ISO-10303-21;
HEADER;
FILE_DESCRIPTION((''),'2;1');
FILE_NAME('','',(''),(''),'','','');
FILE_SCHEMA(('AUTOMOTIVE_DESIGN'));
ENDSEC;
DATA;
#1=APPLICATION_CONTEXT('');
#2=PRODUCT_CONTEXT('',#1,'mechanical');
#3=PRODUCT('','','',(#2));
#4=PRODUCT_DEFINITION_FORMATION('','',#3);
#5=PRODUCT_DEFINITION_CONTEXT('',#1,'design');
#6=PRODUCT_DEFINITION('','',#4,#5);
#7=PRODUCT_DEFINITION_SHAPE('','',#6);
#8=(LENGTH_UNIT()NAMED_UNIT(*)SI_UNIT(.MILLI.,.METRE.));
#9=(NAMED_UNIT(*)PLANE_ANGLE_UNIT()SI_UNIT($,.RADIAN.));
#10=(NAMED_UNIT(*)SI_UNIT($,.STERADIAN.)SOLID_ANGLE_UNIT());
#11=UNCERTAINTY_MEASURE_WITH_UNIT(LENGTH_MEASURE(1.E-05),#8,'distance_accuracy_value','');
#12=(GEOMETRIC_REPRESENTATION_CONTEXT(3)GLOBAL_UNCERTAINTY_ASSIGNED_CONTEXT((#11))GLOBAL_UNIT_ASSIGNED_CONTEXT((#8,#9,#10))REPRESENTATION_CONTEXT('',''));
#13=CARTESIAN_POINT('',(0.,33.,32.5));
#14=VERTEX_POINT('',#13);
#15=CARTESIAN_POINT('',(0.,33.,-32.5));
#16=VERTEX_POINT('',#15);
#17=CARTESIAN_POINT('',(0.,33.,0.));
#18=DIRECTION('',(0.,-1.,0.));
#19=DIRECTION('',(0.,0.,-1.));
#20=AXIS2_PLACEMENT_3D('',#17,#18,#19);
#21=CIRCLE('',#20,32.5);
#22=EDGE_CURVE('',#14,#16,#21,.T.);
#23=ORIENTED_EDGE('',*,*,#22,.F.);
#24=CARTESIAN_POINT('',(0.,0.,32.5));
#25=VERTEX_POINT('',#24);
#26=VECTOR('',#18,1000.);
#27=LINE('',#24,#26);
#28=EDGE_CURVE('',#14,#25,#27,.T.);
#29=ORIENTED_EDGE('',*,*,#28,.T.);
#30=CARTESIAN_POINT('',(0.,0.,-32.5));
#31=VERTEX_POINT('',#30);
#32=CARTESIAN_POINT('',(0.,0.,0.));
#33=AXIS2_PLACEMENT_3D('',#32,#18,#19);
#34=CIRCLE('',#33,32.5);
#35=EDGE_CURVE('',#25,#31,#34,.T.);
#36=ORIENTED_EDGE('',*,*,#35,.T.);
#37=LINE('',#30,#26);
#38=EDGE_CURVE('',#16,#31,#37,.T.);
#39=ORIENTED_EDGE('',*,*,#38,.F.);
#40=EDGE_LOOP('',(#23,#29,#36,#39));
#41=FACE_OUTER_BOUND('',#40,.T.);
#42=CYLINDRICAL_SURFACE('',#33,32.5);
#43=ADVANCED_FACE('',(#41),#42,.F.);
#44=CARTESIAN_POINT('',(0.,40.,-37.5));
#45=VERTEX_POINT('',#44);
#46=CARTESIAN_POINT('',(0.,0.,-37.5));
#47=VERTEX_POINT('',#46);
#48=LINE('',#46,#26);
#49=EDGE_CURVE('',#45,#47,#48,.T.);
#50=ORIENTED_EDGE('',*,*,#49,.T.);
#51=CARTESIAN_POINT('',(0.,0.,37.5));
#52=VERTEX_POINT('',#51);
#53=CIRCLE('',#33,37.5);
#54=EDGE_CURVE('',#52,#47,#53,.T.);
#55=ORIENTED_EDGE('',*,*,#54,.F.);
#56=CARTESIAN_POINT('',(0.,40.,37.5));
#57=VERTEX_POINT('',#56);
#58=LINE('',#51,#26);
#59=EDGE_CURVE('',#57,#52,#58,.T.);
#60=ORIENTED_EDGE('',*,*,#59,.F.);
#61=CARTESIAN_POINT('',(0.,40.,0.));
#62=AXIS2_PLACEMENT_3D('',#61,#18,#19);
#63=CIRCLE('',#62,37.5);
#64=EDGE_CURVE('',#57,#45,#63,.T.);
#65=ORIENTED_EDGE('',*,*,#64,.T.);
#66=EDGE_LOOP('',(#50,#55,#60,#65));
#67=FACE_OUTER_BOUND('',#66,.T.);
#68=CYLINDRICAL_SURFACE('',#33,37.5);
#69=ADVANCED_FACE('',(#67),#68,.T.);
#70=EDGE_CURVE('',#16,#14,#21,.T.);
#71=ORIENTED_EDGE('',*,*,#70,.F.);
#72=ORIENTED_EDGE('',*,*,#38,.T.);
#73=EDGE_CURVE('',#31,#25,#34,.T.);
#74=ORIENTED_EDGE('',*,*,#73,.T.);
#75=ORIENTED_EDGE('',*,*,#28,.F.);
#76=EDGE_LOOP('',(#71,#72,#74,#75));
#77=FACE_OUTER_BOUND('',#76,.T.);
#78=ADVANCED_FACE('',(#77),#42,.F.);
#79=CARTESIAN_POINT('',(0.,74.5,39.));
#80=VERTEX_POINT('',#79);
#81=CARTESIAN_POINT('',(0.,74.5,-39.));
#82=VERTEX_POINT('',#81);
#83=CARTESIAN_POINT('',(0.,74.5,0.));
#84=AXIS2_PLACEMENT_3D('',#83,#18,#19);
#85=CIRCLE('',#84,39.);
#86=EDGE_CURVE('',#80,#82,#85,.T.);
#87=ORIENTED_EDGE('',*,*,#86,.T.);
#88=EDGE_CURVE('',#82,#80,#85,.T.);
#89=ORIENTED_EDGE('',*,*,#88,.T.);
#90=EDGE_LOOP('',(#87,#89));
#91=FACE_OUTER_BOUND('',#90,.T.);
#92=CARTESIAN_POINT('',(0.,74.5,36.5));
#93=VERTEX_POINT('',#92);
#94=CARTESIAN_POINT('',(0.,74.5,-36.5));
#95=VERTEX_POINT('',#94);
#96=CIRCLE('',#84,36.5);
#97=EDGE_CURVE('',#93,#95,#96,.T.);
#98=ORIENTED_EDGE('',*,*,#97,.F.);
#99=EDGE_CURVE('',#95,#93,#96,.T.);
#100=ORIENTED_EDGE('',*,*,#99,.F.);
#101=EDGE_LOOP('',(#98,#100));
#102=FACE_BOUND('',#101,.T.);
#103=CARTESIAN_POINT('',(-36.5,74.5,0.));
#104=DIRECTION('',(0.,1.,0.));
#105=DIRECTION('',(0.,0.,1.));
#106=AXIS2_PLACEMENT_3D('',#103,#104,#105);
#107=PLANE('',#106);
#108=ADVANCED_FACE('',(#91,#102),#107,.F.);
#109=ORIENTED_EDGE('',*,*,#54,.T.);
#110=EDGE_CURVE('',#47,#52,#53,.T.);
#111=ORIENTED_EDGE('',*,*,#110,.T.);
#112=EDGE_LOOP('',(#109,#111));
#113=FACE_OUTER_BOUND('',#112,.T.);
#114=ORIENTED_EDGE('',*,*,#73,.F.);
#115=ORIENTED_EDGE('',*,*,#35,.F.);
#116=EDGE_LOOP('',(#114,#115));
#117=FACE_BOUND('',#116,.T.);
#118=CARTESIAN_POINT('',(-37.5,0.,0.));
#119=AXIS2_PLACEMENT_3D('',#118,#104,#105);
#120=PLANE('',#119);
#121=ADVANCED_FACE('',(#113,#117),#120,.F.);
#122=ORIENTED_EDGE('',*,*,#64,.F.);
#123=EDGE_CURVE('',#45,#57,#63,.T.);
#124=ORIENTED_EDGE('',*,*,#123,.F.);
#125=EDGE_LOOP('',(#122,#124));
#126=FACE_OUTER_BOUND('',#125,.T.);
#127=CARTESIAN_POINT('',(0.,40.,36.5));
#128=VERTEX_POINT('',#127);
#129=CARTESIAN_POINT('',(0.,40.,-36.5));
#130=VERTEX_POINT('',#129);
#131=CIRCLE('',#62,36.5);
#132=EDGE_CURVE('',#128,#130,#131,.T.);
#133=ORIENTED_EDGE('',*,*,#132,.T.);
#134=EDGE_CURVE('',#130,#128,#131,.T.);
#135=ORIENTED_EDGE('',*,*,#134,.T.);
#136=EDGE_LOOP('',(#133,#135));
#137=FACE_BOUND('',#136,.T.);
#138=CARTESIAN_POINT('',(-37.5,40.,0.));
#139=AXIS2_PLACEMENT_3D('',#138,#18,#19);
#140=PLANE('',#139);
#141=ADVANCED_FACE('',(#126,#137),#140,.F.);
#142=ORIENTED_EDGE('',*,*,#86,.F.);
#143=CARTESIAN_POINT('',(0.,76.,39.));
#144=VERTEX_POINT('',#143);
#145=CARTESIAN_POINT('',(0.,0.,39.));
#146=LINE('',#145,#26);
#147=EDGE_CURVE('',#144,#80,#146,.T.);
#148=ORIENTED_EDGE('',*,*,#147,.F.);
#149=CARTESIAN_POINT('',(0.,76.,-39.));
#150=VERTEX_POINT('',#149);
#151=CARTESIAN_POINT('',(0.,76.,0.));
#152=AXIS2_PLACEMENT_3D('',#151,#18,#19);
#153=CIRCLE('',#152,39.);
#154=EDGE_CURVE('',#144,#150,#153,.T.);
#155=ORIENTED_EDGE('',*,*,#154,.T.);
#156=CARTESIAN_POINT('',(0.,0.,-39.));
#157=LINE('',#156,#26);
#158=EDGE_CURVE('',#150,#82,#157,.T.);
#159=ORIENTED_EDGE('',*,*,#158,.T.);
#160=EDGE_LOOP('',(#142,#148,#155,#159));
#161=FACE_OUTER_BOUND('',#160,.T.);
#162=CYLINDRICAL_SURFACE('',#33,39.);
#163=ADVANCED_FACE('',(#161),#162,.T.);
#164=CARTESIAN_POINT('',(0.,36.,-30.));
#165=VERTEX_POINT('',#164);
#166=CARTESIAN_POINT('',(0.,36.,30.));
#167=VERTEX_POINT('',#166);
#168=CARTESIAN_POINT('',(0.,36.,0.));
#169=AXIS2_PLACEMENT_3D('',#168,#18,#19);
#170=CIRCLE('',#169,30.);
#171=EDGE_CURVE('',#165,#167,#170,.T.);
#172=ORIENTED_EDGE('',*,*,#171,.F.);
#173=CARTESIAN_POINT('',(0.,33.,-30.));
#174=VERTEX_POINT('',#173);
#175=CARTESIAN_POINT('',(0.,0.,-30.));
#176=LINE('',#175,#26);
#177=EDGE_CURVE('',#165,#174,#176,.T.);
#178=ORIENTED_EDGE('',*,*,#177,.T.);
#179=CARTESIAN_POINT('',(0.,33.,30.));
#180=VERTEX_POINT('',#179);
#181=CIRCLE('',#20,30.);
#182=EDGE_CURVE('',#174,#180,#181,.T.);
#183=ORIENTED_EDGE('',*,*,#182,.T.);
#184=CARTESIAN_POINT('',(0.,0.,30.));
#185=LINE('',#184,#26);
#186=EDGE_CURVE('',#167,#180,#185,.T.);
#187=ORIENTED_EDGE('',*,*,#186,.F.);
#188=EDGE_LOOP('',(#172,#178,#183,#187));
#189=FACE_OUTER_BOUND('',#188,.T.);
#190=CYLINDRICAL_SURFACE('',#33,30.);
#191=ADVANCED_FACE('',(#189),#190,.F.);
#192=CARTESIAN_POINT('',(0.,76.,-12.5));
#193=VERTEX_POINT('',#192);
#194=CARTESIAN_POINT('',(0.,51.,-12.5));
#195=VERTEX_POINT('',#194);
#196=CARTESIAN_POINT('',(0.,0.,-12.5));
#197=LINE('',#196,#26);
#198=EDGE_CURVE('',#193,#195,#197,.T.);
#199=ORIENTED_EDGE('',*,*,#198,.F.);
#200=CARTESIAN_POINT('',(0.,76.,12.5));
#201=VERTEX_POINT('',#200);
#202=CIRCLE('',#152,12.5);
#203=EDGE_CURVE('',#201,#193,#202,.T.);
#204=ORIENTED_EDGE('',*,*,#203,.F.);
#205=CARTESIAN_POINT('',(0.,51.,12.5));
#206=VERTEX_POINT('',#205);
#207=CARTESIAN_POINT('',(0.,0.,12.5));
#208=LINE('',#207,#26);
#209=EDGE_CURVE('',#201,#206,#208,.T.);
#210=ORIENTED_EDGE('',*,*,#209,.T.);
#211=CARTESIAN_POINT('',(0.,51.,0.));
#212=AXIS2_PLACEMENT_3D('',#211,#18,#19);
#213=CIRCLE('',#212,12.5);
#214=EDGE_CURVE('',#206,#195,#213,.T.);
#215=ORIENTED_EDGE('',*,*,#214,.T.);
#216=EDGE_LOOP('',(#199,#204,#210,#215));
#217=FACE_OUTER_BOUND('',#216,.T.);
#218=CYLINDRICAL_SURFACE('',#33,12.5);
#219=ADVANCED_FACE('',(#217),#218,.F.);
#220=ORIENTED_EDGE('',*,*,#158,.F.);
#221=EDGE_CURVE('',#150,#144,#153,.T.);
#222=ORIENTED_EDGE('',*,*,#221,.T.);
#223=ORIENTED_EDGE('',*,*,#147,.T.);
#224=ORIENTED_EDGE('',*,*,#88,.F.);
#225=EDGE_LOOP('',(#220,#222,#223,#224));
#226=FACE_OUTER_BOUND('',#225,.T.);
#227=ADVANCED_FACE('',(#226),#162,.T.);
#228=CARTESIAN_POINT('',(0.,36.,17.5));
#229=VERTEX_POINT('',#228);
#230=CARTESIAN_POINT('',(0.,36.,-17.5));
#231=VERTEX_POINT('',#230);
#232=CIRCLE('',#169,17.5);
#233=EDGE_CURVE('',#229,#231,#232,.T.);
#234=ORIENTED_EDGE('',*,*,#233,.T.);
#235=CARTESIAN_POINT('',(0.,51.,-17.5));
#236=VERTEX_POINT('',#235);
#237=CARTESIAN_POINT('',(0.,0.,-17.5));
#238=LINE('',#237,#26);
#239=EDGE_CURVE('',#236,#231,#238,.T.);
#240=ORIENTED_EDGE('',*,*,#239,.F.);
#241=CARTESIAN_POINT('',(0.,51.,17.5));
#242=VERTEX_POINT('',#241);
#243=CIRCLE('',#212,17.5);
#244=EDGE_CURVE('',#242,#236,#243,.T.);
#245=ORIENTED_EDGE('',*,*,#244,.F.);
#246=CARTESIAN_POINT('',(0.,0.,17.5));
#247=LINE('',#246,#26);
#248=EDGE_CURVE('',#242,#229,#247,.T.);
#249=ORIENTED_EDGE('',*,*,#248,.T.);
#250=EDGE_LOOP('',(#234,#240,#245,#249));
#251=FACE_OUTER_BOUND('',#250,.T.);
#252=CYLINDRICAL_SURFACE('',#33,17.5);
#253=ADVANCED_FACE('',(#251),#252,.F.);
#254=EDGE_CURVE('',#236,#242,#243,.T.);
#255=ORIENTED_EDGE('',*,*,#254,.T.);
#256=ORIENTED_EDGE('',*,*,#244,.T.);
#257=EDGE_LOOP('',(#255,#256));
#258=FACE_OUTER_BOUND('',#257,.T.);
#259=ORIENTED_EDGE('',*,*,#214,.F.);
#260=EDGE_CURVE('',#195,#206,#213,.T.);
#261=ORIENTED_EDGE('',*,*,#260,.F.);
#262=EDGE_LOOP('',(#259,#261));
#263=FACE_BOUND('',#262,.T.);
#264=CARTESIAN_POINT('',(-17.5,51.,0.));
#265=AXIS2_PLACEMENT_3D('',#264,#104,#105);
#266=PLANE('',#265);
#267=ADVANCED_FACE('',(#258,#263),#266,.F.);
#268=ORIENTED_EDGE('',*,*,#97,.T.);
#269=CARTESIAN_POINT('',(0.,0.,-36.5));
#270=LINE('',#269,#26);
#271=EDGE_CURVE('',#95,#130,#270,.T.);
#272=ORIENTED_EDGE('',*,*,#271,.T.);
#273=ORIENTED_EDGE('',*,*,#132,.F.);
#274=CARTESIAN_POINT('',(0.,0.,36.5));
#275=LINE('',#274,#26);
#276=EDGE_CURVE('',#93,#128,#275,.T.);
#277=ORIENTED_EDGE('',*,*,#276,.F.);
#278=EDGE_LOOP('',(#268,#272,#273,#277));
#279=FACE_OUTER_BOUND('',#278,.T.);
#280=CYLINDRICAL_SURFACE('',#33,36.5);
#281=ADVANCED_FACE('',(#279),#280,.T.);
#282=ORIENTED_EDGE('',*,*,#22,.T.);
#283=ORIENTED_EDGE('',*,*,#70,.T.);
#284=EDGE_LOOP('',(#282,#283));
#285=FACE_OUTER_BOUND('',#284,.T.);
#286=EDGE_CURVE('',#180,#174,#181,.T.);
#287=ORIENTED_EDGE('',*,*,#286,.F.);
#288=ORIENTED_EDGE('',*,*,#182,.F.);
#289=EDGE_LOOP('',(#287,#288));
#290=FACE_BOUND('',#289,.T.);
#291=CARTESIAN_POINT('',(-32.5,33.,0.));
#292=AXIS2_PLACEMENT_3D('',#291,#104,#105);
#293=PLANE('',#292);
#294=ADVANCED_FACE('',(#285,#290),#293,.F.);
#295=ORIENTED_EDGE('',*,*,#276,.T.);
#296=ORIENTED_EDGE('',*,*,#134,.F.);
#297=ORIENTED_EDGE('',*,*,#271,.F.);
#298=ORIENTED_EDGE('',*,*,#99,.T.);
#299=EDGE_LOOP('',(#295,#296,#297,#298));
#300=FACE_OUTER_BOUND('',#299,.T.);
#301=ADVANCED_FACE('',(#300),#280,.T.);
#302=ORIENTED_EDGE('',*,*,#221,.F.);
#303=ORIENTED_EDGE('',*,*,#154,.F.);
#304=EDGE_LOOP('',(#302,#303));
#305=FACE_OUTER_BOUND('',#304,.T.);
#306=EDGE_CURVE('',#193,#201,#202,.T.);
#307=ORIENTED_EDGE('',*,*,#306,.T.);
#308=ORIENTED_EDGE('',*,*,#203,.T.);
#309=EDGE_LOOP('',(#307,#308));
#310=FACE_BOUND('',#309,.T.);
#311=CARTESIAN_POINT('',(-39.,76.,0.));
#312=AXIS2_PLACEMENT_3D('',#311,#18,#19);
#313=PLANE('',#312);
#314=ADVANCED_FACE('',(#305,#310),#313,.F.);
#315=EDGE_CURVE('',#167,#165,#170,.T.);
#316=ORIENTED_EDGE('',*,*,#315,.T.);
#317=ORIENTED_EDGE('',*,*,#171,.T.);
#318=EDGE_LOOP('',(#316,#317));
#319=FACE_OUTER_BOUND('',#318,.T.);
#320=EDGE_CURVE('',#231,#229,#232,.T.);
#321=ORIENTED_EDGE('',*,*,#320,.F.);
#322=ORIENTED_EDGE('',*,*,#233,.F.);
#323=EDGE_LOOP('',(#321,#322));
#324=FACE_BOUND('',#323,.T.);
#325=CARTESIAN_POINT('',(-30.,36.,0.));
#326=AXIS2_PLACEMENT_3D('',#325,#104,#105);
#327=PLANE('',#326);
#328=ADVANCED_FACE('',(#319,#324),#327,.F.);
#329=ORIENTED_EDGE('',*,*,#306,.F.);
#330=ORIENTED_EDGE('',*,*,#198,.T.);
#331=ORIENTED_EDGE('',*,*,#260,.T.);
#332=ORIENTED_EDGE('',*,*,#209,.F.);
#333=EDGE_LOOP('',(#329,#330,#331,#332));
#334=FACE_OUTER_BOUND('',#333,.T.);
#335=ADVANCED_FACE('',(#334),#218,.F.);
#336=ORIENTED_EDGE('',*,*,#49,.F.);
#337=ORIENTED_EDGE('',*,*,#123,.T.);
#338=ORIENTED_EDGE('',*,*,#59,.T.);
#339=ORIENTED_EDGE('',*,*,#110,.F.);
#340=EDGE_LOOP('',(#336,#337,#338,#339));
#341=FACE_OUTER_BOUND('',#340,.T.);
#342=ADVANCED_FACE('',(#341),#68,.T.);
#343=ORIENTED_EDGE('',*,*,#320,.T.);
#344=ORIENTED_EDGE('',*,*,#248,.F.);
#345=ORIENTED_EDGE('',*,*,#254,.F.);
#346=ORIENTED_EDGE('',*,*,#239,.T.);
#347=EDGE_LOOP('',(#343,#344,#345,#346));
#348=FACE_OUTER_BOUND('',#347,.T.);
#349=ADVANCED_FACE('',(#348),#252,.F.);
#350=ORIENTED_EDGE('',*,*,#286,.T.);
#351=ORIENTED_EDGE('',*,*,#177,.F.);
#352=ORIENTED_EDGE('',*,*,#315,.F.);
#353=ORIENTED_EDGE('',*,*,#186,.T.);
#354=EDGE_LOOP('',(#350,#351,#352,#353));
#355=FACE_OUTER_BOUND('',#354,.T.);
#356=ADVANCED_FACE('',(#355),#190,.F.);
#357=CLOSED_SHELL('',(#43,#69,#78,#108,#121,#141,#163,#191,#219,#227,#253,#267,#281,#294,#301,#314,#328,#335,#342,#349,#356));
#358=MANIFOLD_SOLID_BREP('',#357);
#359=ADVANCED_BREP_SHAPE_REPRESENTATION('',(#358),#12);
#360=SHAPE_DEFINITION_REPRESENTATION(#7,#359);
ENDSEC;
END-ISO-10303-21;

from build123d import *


with BuildPart() as part:
    # 草图1 → 旋转1 (revolve)
    with BuildSketch(Plane.XY, mode=Mode.PRIVATE) as revolve_1_sk:
        Polygon((-37.5, 0), (-37.5, 40), (-36.5, 40), (-36.5, 74.5), (-39, 74.5), (-39, 76), (-17.5, 76), (-12.5, 76), (-12.5, 51), (-17.5, 51), (-17.5, 36), (-30, 36), (-30, 33), (-32.5, 33), (-32.5, 0), align=None)
    revolve(revolve_1_sk.sketch.rotate(Axis((0, 0, 0), (0, 1, 0)), 270), axis=Axis((0, 0, 0), (0, 1, 0)))


solid = part.part
